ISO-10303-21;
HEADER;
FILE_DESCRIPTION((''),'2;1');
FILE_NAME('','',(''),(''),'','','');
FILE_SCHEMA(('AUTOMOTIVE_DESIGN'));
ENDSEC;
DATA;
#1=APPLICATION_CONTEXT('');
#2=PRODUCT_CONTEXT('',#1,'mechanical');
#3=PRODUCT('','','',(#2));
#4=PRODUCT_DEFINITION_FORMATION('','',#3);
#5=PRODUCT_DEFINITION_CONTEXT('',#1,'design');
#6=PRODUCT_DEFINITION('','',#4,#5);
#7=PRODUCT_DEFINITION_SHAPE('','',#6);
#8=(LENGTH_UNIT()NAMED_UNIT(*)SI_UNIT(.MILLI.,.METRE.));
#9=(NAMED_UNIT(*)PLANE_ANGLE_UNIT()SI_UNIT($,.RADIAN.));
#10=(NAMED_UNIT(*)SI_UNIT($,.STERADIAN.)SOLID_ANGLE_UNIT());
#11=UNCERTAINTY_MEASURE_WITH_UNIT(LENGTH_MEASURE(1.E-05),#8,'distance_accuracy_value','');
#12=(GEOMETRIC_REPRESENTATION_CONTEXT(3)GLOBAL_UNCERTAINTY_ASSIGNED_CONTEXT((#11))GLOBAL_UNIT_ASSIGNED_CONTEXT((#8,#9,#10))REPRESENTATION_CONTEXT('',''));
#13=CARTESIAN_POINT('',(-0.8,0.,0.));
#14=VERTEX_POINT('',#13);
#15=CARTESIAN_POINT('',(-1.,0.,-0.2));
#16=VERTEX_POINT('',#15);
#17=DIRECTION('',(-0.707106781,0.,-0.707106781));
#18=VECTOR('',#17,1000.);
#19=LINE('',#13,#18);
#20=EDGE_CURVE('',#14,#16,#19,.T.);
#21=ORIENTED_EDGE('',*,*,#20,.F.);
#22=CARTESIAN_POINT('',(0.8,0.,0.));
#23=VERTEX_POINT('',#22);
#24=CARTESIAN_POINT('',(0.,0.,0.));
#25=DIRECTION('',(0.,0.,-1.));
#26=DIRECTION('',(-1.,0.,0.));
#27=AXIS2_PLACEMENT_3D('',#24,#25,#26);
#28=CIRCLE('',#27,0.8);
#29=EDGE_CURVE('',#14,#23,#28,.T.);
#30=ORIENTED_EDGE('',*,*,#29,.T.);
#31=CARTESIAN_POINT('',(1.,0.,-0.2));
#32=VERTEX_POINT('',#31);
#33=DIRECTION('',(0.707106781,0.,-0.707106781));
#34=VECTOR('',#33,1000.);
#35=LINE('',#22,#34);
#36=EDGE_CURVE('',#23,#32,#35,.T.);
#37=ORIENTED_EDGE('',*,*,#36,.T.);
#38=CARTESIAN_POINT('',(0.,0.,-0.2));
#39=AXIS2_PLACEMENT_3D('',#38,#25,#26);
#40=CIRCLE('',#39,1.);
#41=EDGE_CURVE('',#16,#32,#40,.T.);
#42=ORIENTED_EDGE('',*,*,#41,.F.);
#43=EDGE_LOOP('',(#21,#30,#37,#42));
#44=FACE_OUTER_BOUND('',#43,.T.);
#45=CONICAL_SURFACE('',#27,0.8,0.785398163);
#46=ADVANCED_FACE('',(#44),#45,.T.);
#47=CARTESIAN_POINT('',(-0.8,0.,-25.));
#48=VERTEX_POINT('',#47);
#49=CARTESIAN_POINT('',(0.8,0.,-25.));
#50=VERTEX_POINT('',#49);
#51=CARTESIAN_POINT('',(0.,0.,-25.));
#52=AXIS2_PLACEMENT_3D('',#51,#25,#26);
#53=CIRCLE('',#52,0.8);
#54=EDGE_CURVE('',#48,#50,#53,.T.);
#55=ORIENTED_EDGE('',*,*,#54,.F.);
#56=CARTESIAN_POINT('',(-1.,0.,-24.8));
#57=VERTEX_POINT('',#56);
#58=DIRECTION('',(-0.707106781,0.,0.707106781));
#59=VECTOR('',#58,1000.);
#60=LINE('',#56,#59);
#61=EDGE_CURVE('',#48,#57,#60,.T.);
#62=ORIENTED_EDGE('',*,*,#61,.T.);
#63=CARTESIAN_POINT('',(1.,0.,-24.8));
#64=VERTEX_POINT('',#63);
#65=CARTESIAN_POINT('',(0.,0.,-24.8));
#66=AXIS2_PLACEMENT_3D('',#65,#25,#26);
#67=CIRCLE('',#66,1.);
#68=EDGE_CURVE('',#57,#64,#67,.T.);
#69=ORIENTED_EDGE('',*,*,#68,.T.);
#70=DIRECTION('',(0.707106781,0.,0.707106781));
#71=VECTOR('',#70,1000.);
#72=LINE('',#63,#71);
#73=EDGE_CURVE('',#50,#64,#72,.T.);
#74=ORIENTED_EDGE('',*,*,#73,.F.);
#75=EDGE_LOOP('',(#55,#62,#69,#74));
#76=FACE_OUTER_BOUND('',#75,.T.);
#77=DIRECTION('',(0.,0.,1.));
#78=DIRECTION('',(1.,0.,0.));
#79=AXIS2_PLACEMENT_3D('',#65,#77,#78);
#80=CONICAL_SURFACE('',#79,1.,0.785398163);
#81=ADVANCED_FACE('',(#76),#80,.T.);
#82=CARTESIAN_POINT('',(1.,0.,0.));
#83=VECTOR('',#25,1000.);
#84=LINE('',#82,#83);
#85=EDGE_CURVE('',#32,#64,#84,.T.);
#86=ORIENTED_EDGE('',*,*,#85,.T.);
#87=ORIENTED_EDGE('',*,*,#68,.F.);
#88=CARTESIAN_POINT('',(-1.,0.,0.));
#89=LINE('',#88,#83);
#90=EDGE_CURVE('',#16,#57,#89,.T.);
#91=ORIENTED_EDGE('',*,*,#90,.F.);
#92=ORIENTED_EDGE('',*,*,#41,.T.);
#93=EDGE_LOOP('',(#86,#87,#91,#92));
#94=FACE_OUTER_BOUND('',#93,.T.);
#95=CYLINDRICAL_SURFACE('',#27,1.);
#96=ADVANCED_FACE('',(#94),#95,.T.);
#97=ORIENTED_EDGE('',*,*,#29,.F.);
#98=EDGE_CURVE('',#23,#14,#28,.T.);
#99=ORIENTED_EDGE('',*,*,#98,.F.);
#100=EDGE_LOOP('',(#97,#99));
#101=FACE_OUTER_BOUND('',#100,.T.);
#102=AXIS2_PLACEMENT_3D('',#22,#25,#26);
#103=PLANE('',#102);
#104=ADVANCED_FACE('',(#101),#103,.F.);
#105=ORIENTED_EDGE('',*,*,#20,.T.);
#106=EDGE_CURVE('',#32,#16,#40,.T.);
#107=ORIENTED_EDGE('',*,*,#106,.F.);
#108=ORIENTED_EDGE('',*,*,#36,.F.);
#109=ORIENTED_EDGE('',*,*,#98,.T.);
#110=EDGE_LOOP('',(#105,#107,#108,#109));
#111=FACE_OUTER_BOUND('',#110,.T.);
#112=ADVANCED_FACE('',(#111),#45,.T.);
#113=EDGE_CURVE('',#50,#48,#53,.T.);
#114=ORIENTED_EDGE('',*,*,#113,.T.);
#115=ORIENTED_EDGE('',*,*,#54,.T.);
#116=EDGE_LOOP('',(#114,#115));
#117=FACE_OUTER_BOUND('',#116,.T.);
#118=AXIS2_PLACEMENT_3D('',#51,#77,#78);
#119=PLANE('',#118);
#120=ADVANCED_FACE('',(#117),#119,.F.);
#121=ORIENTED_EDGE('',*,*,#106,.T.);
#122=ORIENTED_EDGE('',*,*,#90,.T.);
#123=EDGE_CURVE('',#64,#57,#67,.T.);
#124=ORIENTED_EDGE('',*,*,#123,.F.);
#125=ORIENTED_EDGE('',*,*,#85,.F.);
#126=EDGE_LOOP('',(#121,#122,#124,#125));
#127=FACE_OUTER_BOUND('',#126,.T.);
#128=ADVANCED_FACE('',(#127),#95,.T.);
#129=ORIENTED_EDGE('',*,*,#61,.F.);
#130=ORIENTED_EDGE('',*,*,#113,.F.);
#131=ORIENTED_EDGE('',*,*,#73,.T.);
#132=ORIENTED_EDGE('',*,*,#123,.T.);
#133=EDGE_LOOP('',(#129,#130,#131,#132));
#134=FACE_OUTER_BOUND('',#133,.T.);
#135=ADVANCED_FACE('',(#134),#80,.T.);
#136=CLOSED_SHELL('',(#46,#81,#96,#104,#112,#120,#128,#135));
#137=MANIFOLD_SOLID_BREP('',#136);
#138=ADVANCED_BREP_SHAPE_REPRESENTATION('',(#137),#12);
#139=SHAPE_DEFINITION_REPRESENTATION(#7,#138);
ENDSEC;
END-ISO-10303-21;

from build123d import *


with BuildPart() as part:
    # 草图1 → 旋转1 (revolve)
    with BuildSketch(Plane(origin=(0, 0, 0), x_dir=(1, 0, 0), z_dir=(0, 1, 0)), mode=Mode.PRIVATE) as revolve_1_sk:
        Polygon((0, 25), (0.8, 25), (1, 24.8), (1, 0.2), (0.8, 0), (0, 0), align=None)
    revolve(revolve_1_sk.sketch.rotate(Axis((0, 0, 0), (0, 0, -1)), 180), axis=Axis((0, 0, 0), (0, 0, -1)))


solid = part.part
